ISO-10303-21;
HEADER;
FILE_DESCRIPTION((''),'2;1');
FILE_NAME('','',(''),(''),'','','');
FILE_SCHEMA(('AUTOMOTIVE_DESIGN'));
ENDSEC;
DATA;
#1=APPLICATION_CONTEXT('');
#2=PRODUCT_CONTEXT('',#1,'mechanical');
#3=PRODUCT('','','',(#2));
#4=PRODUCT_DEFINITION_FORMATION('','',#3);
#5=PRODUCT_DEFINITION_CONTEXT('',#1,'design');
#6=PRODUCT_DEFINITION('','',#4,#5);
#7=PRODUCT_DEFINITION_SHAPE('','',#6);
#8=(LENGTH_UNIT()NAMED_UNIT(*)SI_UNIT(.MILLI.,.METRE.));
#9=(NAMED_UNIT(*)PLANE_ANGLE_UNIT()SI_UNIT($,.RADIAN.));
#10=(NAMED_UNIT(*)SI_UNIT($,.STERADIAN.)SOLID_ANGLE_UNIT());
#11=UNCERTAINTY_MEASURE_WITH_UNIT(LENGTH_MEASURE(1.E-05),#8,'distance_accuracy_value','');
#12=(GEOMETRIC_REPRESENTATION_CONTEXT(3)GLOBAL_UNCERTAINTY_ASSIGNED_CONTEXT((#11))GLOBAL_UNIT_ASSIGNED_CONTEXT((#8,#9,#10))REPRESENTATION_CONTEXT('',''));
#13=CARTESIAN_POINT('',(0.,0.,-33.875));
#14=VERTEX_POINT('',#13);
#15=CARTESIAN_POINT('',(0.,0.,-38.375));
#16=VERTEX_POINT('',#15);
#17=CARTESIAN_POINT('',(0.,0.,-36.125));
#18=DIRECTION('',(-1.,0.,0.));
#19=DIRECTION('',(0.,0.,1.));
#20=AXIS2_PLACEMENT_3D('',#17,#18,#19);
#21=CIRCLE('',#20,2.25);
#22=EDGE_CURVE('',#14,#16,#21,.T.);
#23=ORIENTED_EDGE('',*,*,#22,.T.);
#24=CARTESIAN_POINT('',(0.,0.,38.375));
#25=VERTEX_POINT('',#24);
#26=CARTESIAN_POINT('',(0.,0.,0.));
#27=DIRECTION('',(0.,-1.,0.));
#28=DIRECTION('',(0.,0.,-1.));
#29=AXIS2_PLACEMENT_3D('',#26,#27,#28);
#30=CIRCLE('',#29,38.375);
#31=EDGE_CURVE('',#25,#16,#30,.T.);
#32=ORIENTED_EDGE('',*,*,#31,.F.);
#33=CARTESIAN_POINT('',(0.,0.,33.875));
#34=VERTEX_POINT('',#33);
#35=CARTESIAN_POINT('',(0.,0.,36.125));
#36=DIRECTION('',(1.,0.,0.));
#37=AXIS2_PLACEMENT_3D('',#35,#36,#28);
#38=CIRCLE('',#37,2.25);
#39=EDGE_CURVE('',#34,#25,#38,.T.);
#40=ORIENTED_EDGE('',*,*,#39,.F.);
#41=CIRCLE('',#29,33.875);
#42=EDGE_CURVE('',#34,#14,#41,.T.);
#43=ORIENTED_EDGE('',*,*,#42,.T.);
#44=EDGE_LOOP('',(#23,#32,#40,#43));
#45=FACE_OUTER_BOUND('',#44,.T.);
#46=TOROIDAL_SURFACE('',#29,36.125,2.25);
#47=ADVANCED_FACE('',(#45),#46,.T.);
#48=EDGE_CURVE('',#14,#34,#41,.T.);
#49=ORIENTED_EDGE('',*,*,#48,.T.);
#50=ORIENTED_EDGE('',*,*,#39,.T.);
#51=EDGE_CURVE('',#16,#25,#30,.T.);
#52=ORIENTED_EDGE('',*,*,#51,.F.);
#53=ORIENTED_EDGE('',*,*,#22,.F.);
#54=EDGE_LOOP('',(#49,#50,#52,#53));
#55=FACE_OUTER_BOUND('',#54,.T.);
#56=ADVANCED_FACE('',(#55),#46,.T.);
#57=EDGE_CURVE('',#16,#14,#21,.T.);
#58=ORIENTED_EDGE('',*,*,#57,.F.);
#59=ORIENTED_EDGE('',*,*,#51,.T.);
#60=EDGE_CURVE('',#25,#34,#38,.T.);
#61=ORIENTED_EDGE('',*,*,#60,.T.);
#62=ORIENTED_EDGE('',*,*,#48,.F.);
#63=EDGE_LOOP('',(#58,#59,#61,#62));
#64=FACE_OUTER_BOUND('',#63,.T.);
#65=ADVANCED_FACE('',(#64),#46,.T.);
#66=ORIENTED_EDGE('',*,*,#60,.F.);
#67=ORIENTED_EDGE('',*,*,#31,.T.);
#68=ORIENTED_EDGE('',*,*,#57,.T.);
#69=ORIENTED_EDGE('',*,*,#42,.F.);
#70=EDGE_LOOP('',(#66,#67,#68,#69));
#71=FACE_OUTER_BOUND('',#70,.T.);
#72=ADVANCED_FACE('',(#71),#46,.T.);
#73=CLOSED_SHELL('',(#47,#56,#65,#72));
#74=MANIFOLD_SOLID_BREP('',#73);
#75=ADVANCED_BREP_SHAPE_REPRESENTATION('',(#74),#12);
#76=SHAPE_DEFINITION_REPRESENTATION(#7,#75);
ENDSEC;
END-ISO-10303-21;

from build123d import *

# Parameters (mm, degrees)
SKETCH_1_R = 2.25


with BuildPart() as part:
    # 草图1 → 旋转1 (revolve)
    with BuildSketch(Plane.XY, mode=Mode.PRIVATE) as revolve_1_sk:
        with Locations((-36.125, 0)):
            Circle(SKETCH_1_R)
    revolve(revolve_1_sk.sketch.rotate(Axis((0, 0, 0), (0, 1, 0)), 270), axis=Axis((0, 0, 0), (0, 1, 0)))


solid = part.part
